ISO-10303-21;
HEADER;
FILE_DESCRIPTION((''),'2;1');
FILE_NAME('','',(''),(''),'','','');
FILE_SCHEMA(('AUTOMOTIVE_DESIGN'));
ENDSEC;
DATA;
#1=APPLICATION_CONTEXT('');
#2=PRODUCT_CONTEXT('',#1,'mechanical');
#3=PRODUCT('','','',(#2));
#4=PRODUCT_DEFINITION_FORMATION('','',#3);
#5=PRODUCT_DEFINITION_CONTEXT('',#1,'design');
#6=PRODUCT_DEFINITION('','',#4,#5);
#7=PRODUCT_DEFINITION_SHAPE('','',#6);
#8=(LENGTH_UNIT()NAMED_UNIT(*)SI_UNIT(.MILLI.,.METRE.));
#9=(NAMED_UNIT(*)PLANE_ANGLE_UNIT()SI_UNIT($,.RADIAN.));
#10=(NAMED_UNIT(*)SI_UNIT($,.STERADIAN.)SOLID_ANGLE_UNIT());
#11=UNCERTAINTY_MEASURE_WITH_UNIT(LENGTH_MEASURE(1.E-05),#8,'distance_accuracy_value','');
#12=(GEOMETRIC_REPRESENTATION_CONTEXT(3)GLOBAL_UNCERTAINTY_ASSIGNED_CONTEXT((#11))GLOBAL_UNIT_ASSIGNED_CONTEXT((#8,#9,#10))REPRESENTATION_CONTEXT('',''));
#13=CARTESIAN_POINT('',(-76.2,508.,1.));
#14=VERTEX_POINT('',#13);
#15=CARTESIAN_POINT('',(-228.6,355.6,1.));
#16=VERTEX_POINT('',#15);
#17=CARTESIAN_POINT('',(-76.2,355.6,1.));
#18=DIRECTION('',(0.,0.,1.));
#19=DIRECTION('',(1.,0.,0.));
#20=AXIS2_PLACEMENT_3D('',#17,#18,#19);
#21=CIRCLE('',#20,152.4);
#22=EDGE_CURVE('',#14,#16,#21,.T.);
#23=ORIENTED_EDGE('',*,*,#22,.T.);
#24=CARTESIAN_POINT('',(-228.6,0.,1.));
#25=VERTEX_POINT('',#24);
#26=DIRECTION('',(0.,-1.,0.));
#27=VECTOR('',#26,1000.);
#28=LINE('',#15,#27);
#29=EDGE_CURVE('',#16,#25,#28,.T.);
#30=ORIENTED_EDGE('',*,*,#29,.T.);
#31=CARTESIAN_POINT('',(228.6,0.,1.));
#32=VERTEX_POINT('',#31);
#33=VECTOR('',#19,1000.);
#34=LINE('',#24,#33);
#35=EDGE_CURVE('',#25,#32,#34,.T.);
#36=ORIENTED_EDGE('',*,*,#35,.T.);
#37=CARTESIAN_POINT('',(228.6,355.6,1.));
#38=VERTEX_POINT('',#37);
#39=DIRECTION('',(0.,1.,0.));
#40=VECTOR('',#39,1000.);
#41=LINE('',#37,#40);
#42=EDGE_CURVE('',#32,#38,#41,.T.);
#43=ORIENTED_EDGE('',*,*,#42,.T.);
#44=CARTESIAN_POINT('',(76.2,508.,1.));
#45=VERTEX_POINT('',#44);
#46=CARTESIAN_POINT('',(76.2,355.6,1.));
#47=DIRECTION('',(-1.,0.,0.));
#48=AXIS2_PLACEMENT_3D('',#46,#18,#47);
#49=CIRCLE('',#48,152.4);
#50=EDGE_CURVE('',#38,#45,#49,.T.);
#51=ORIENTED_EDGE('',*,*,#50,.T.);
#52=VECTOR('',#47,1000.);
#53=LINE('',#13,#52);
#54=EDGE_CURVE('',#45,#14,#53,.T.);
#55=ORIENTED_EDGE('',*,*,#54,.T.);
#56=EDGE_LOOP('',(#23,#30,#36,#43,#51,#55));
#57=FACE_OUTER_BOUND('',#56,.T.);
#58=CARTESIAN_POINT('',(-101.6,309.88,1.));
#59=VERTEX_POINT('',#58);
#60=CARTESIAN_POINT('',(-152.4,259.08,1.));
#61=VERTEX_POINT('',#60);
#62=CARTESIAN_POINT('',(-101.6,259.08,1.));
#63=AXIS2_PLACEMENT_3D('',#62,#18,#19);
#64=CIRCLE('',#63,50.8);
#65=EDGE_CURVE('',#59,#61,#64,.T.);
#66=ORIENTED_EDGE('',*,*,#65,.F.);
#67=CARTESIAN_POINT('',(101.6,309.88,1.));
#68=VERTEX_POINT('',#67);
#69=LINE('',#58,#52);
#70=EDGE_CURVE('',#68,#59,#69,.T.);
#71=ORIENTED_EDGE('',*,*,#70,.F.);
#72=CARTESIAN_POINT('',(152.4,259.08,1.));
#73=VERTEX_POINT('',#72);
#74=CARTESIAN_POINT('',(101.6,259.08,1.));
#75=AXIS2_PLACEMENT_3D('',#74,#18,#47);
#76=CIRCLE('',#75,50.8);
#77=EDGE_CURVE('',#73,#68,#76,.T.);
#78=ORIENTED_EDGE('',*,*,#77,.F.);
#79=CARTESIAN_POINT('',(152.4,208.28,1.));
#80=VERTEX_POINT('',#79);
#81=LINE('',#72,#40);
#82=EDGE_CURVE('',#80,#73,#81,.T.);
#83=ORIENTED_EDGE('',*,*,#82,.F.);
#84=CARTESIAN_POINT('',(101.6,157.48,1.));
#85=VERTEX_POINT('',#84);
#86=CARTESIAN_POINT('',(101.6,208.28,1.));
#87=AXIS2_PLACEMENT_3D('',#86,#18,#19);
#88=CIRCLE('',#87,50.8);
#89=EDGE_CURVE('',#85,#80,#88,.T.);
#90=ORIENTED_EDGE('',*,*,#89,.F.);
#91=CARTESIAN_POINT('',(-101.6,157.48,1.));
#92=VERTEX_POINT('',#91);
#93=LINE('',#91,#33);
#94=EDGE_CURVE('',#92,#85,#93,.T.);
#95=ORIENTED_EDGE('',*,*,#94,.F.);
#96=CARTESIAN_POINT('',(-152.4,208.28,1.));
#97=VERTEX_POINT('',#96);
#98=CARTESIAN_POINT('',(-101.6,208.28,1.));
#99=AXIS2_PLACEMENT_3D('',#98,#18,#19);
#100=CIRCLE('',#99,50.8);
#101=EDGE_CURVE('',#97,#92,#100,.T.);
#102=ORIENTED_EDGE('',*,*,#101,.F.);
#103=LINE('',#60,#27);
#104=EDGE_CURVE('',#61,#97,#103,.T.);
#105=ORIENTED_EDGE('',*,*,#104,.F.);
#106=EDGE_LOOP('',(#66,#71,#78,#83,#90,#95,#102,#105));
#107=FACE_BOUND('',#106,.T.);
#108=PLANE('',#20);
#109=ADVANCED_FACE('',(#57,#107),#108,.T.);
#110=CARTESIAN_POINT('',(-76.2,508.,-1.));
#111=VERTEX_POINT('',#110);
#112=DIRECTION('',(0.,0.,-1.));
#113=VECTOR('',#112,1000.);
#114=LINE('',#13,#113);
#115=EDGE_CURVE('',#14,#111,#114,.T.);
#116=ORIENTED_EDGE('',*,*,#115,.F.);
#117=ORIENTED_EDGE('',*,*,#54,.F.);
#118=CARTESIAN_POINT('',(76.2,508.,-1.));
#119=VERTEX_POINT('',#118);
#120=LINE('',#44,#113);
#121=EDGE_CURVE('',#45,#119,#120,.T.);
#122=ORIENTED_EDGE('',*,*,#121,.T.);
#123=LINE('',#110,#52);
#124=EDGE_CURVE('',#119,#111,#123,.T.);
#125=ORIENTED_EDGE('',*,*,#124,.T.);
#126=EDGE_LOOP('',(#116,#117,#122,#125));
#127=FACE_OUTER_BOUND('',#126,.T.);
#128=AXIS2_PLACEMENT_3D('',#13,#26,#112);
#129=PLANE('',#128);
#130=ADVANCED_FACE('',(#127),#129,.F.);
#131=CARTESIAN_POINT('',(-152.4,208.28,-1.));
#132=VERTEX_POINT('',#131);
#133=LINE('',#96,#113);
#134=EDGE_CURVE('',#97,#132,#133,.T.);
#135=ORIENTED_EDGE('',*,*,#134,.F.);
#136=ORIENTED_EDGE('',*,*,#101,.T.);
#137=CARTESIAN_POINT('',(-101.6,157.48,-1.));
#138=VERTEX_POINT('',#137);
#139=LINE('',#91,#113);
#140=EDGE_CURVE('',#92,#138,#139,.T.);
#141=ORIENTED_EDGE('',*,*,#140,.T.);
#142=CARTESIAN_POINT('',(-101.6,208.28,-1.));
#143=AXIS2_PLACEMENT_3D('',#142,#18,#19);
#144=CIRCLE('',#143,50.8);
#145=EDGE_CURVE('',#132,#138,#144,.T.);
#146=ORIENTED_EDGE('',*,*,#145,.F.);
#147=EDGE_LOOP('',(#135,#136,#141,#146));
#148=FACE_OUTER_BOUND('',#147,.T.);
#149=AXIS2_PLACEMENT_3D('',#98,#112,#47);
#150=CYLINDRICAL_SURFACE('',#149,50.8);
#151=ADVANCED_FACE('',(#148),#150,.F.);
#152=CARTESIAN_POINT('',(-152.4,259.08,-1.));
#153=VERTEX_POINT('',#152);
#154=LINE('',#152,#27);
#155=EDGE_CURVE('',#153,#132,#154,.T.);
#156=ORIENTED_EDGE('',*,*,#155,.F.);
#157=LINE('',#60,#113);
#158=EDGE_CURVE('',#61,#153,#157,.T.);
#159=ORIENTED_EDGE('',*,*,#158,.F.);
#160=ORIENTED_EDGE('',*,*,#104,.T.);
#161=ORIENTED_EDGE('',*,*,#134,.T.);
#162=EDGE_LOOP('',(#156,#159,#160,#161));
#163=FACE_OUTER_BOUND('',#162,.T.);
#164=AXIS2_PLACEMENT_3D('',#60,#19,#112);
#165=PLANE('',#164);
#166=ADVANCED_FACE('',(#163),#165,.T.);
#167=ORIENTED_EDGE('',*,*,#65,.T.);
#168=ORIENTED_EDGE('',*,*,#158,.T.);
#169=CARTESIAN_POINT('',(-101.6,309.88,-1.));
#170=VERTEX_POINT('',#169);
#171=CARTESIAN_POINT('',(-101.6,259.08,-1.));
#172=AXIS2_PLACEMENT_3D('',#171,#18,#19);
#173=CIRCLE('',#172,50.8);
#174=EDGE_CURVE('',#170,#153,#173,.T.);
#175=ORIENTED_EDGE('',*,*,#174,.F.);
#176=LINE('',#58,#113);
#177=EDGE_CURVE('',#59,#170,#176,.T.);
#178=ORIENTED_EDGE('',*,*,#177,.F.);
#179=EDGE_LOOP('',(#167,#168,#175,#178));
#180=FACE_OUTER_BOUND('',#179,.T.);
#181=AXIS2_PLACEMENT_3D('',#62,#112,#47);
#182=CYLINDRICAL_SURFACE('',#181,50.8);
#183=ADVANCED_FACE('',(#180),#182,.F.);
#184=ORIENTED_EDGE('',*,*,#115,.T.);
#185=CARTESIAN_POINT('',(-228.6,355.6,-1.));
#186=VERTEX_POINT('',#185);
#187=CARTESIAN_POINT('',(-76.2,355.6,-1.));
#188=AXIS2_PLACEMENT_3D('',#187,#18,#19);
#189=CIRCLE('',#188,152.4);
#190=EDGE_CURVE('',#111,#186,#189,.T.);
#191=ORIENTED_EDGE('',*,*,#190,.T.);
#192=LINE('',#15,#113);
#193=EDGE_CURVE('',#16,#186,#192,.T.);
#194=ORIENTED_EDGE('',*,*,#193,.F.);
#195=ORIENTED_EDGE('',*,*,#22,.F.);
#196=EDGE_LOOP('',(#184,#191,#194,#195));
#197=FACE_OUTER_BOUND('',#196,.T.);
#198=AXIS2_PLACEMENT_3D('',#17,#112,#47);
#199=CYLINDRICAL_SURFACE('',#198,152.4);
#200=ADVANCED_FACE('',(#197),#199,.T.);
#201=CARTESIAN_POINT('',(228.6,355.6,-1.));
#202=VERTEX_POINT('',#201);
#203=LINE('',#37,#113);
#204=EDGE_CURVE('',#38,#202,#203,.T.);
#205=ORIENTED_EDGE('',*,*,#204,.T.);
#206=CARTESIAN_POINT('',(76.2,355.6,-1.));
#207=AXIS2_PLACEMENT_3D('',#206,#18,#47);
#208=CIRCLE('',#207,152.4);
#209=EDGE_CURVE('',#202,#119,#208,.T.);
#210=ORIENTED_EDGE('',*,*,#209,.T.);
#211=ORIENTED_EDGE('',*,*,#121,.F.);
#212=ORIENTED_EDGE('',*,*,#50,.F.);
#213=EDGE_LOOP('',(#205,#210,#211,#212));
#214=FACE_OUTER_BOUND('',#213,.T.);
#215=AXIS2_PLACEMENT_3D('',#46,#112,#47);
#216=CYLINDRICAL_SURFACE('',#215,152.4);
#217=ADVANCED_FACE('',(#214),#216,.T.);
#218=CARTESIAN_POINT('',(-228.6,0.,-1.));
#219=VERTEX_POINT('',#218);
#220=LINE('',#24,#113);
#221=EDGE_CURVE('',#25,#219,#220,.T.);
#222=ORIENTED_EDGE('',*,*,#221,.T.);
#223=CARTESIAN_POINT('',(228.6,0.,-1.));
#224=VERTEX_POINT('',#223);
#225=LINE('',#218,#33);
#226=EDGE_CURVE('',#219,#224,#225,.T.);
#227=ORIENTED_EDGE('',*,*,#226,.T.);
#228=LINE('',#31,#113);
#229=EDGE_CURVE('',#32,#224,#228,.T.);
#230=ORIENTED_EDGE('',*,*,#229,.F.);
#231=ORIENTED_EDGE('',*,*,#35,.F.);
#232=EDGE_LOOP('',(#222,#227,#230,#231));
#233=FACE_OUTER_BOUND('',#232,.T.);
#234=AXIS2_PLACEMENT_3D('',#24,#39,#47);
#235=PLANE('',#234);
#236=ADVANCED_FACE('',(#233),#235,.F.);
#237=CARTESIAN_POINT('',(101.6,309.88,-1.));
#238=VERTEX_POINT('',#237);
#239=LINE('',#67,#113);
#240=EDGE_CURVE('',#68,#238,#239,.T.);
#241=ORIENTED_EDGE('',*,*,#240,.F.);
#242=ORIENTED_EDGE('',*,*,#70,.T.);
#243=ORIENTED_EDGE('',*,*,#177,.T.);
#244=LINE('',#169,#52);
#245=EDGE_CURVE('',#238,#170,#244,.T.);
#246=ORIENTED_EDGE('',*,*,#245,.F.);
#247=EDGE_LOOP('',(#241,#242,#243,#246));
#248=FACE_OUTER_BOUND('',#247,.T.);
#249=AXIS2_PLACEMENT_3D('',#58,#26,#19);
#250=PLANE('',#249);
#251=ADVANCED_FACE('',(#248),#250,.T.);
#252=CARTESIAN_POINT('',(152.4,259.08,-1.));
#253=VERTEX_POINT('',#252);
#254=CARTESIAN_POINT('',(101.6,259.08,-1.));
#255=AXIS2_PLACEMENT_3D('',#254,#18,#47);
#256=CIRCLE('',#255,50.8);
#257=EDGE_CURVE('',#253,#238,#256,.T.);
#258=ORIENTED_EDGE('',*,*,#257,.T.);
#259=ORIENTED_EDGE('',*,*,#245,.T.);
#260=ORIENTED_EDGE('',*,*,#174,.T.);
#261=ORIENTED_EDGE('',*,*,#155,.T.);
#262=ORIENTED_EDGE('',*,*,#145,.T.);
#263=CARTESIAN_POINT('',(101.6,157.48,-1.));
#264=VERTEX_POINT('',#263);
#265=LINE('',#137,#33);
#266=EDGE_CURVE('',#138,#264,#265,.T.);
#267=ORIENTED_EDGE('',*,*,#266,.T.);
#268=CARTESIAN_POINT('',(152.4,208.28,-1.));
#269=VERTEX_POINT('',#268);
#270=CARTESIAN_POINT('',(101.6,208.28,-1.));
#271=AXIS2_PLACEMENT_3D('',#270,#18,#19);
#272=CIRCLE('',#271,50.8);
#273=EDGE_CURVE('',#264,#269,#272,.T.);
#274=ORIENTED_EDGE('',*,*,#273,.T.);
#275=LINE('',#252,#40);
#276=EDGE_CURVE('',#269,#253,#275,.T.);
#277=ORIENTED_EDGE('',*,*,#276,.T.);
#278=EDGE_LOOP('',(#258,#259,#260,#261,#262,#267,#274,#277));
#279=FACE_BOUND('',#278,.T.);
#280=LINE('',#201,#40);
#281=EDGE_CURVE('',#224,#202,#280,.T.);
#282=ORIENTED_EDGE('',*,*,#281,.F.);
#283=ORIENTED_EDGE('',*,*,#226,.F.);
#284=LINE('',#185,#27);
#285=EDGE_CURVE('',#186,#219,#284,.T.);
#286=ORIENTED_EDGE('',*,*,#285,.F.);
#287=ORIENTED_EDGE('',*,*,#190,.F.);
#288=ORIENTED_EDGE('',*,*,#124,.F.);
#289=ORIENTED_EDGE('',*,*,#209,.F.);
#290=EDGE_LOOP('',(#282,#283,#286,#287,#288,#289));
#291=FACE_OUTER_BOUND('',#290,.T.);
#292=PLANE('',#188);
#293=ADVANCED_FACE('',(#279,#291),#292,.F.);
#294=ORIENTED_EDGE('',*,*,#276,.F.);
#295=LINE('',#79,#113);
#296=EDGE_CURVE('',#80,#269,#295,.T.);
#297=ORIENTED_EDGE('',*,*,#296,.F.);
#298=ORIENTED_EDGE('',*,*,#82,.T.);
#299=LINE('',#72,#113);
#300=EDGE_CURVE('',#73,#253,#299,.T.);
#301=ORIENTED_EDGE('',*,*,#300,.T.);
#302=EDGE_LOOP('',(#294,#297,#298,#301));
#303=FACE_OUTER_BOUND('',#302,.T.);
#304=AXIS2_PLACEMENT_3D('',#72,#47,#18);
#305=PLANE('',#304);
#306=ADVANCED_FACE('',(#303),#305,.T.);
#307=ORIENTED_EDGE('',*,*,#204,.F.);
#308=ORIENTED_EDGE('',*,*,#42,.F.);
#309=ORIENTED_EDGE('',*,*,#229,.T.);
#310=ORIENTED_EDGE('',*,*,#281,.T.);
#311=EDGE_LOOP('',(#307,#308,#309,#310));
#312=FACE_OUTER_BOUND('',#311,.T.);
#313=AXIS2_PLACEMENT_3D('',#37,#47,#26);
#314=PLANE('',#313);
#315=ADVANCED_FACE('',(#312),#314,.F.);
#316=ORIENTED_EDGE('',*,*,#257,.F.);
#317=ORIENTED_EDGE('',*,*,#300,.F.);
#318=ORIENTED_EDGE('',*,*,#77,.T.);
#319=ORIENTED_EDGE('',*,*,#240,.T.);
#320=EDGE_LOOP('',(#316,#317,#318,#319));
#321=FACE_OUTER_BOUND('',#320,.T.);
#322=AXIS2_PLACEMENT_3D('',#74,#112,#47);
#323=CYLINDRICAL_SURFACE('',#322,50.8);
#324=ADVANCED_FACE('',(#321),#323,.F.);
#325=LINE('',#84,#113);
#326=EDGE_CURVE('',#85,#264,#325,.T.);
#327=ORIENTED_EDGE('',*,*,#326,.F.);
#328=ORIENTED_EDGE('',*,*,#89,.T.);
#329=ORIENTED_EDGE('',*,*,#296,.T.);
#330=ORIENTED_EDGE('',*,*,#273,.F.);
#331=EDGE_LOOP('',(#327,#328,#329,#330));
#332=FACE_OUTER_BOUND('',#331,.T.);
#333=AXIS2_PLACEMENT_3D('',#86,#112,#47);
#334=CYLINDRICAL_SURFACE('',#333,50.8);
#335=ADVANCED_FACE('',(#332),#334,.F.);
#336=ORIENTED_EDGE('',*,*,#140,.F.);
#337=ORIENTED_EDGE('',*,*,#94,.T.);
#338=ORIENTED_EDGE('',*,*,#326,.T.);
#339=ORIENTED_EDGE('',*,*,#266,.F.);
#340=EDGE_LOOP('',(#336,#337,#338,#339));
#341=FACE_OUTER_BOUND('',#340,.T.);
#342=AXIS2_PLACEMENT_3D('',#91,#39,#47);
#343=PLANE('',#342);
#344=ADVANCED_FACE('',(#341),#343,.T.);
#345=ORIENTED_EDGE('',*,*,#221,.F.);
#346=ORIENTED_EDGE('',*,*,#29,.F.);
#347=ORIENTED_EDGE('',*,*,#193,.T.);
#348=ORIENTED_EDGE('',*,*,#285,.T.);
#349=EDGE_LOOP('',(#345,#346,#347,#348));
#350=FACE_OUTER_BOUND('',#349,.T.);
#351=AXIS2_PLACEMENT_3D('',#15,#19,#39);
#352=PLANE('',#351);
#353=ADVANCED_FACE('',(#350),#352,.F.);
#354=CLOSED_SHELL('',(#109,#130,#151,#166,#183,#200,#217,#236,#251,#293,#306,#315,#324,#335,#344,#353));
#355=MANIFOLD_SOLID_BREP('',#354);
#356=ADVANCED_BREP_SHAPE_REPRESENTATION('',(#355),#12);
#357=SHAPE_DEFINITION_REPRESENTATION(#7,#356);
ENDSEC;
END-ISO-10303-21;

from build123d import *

# Parameters (mm, degrees)
BOSS_EXTRUDE1_DEPTH = 1


with BuildPart() as part:
    # Sketch1 → Boss-Extrude1 (new, symmetric)
    with BuildSketch(Plane.XY):
        with BuildLine():
            Line((-76.2, 508), (76.2, 508))
            ThreePointArc((76.2, 508), (183.963073453, 463.363073453), (228.6, 355.6))
            Line((228.6, 355.6), (228.6, 0))
            Line((228.6, 0), (-228.6, 0))
            Line((-228.6, 0), (-228.6, 355.6))
            ThreePointArc((-228.6, 355.6), (-183.963073453, 463.363073453), (-76.2, 508))
        make_face()
        with BuildLine():
            Line((-101.6, 309.88), (101.6, 309.88))
            ThreePointArc((101.6, 309.88), (137.521024484, 295.001024484), (152.4, 259.08))
            Line((152.4, 259.08), (152.4, 208.28))
            ThreePointArc((152.4, 208.28), (137.521024484, 172.358975516), (101.6, 157.48))
            Line((101.6, 157.48), (-101.6, 157.48))
            ThreePointArc((-101.6, 157.48), (-137.521024484, 172.358975516), (-152.4, 208.28))
            Line((-152.4, 208.28), (-152.4, 259.08))
            ThreePointArc((-152.4, 259.08), (-137.521024484, 295.001024484), (-101.6, 309.88))
        make_face(mode=Mode.SUBTRACT)
    extrude(amount=BOSS_EXTRUDE1_DEPTH, both=True)


solid = part.part
